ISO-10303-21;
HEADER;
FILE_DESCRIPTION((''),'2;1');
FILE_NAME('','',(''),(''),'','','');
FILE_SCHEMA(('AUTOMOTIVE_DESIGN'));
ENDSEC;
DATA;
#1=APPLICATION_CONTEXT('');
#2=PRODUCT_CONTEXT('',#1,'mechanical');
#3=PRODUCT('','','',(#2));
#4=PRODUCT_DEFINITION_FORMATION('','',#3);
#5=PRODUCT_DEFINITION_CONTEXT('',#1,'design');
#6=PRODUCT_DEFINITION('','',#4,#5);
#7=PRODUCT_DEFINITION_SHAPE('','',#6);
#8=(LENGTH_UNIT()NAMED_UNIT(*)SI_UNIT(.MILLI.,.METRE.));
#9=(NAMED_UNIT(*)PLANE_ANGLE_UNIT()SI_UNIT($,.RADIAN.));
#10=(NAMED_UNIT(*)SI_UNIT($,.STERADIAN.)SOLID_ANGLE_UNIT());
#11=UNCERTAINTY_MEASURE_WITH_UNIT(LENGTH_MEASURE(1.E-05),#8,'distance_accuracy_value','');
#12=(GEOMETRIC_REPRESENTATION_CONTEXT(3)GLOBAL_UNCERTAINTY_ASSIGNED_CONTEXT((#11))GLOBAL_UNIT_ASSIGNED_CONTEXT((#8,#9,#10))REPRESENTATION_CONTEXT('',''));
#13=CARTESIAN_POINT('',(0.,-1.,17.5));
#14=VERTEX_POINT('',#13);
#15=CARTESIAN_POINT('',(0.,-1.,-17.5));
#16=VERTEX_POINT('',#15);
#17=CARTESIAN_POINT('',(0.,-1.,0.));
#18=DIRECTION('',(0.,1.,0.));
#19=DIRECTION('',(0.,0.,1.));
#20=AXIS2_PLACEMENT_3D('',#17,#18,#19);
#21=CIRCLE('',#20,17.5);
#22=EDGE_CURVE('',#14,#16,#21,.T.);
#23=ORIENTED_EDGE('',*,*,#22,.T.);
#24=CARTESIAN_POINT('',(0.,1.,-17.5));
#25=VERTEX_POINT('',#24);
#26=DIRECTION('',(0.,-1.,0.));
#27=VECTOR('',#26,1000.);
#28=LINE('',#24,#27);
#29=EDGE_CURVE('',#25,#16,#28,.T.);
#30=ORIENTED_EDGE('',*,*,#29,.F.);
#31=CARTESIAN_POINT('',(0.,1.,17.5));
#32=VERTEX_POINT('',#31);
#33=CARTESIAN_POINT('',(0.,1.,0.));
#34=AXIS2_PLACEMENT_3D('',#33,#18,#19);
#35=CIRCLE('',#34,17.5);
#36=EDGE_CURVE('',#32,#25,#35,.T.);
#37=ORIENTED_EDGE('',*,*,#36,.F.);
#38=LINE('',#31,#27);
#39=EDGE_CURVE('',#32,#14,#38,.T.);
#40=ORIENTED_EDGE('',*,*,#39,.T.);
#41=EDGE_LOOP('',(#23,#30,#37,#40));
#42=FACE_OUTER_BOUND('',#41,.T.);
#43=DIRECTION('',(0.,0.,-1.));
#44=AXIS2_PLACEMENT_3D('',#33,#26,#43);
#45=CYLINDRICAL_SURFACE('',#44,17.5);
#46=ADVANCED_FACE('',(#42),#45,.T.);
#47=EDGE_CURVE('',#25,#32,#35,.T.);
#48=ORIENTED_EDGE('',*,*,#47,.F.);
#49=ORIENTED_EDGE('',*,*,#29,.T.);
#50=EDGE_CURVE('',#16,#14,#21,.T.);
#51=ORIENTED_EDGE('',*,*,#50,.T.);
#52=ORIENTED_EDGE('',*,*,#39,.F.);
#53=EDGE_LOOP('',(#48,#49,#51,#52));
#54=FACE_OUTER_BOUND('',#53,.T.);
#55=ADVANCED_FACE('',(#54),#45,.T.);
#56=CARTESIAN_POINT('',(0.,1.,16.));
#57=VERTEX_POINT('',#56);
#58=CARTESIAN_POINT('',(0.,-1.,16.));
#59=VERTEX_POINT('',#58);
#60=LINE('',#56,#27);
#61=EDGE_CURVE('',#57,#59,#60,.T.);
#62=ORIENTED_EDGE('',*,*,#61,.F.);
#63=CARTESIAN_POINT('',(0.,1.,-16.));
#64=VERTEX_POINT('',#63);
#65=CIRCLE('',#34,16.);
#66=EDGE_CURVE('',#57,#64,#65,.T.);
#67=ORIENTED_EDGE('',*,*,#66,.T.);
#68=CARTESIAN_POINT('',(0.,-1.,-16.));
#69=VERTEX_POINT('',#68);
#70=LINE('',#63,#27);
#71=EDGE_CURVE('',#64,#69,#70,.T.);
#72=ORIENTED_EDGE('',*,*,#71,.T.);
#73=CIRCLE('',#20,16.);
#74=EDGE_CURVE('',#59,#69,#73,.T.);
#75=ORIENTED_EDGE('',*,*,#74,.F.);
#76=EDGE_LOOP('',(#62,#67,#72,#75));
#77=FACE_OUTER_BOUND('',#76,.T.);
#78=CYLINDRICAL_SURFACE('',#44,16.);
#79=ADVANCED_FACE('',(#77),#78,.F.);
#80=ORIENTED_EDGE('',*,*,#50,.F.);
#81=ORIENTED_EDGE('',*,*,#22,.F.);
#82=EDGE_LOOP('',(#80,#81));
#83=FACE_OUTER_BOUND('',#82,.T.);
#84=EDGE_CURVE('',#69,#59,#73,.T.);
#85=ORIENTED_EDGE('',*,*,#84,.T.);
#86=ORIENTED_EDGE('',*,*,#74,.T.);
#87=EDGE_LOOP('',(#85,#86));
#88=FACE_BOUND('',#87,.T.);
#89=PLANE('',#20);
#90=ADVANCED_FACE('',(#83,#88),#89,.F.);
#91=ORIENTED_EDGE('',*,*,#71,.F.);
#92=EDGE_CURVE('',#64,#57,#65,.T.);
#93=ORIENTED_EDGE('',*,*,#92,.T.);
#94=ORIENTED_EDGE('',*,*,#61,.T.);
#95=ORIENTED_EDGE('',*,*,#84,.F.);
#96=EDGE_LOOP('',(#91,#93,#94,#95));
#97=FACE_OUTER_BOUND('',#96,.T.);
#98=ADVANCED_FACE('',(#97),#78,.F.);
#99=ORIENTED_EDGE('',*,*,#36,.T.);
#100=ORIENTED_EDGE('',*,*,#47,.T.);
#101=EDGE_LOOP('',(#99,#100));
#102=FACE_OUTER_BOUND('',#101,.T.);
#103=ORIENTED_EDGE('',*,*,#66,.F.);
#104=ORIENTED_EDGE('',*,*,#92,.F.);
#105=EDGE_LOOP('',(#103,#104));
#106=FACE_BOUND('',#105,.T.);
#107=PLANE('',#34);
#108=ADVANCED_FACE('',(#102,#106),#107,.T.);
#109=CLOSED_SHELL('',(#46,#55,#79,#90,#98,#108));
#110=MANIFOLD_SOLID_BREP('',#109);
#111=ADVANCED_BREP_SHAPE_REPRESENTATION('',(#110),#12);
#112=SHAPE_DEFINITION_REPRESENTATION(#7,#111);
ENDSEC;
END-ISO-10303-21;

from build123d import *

# Parameters (mm, degrees)
SKETCH1_R           = 17.5
SKETCH1_R_2         = 16
BOSS_EXTRUDE1_DEPTH = 1


with BuildPart() as part:
    # Sketch1 → Boss-Extrude1 (new, symmetric)
    with BuildSketch(Plane(origin=(0, 0, 0), x_dir=(1, 0, 0), z_dir=(0, 1, 0))):
        with Locations(Location((0, 0, 0), (0, 0, 270))):
            Circle(SKETCH1_R)
        with Locations(Location((0, 0, 0), (0, 0, 270))):
            Circle(SKETCH1_R_2, mode=Mode.SUBTRACT)
    extrude(amount=BOSS_EXTRUDE1_DEPTH, both=True)


solid = part.part
